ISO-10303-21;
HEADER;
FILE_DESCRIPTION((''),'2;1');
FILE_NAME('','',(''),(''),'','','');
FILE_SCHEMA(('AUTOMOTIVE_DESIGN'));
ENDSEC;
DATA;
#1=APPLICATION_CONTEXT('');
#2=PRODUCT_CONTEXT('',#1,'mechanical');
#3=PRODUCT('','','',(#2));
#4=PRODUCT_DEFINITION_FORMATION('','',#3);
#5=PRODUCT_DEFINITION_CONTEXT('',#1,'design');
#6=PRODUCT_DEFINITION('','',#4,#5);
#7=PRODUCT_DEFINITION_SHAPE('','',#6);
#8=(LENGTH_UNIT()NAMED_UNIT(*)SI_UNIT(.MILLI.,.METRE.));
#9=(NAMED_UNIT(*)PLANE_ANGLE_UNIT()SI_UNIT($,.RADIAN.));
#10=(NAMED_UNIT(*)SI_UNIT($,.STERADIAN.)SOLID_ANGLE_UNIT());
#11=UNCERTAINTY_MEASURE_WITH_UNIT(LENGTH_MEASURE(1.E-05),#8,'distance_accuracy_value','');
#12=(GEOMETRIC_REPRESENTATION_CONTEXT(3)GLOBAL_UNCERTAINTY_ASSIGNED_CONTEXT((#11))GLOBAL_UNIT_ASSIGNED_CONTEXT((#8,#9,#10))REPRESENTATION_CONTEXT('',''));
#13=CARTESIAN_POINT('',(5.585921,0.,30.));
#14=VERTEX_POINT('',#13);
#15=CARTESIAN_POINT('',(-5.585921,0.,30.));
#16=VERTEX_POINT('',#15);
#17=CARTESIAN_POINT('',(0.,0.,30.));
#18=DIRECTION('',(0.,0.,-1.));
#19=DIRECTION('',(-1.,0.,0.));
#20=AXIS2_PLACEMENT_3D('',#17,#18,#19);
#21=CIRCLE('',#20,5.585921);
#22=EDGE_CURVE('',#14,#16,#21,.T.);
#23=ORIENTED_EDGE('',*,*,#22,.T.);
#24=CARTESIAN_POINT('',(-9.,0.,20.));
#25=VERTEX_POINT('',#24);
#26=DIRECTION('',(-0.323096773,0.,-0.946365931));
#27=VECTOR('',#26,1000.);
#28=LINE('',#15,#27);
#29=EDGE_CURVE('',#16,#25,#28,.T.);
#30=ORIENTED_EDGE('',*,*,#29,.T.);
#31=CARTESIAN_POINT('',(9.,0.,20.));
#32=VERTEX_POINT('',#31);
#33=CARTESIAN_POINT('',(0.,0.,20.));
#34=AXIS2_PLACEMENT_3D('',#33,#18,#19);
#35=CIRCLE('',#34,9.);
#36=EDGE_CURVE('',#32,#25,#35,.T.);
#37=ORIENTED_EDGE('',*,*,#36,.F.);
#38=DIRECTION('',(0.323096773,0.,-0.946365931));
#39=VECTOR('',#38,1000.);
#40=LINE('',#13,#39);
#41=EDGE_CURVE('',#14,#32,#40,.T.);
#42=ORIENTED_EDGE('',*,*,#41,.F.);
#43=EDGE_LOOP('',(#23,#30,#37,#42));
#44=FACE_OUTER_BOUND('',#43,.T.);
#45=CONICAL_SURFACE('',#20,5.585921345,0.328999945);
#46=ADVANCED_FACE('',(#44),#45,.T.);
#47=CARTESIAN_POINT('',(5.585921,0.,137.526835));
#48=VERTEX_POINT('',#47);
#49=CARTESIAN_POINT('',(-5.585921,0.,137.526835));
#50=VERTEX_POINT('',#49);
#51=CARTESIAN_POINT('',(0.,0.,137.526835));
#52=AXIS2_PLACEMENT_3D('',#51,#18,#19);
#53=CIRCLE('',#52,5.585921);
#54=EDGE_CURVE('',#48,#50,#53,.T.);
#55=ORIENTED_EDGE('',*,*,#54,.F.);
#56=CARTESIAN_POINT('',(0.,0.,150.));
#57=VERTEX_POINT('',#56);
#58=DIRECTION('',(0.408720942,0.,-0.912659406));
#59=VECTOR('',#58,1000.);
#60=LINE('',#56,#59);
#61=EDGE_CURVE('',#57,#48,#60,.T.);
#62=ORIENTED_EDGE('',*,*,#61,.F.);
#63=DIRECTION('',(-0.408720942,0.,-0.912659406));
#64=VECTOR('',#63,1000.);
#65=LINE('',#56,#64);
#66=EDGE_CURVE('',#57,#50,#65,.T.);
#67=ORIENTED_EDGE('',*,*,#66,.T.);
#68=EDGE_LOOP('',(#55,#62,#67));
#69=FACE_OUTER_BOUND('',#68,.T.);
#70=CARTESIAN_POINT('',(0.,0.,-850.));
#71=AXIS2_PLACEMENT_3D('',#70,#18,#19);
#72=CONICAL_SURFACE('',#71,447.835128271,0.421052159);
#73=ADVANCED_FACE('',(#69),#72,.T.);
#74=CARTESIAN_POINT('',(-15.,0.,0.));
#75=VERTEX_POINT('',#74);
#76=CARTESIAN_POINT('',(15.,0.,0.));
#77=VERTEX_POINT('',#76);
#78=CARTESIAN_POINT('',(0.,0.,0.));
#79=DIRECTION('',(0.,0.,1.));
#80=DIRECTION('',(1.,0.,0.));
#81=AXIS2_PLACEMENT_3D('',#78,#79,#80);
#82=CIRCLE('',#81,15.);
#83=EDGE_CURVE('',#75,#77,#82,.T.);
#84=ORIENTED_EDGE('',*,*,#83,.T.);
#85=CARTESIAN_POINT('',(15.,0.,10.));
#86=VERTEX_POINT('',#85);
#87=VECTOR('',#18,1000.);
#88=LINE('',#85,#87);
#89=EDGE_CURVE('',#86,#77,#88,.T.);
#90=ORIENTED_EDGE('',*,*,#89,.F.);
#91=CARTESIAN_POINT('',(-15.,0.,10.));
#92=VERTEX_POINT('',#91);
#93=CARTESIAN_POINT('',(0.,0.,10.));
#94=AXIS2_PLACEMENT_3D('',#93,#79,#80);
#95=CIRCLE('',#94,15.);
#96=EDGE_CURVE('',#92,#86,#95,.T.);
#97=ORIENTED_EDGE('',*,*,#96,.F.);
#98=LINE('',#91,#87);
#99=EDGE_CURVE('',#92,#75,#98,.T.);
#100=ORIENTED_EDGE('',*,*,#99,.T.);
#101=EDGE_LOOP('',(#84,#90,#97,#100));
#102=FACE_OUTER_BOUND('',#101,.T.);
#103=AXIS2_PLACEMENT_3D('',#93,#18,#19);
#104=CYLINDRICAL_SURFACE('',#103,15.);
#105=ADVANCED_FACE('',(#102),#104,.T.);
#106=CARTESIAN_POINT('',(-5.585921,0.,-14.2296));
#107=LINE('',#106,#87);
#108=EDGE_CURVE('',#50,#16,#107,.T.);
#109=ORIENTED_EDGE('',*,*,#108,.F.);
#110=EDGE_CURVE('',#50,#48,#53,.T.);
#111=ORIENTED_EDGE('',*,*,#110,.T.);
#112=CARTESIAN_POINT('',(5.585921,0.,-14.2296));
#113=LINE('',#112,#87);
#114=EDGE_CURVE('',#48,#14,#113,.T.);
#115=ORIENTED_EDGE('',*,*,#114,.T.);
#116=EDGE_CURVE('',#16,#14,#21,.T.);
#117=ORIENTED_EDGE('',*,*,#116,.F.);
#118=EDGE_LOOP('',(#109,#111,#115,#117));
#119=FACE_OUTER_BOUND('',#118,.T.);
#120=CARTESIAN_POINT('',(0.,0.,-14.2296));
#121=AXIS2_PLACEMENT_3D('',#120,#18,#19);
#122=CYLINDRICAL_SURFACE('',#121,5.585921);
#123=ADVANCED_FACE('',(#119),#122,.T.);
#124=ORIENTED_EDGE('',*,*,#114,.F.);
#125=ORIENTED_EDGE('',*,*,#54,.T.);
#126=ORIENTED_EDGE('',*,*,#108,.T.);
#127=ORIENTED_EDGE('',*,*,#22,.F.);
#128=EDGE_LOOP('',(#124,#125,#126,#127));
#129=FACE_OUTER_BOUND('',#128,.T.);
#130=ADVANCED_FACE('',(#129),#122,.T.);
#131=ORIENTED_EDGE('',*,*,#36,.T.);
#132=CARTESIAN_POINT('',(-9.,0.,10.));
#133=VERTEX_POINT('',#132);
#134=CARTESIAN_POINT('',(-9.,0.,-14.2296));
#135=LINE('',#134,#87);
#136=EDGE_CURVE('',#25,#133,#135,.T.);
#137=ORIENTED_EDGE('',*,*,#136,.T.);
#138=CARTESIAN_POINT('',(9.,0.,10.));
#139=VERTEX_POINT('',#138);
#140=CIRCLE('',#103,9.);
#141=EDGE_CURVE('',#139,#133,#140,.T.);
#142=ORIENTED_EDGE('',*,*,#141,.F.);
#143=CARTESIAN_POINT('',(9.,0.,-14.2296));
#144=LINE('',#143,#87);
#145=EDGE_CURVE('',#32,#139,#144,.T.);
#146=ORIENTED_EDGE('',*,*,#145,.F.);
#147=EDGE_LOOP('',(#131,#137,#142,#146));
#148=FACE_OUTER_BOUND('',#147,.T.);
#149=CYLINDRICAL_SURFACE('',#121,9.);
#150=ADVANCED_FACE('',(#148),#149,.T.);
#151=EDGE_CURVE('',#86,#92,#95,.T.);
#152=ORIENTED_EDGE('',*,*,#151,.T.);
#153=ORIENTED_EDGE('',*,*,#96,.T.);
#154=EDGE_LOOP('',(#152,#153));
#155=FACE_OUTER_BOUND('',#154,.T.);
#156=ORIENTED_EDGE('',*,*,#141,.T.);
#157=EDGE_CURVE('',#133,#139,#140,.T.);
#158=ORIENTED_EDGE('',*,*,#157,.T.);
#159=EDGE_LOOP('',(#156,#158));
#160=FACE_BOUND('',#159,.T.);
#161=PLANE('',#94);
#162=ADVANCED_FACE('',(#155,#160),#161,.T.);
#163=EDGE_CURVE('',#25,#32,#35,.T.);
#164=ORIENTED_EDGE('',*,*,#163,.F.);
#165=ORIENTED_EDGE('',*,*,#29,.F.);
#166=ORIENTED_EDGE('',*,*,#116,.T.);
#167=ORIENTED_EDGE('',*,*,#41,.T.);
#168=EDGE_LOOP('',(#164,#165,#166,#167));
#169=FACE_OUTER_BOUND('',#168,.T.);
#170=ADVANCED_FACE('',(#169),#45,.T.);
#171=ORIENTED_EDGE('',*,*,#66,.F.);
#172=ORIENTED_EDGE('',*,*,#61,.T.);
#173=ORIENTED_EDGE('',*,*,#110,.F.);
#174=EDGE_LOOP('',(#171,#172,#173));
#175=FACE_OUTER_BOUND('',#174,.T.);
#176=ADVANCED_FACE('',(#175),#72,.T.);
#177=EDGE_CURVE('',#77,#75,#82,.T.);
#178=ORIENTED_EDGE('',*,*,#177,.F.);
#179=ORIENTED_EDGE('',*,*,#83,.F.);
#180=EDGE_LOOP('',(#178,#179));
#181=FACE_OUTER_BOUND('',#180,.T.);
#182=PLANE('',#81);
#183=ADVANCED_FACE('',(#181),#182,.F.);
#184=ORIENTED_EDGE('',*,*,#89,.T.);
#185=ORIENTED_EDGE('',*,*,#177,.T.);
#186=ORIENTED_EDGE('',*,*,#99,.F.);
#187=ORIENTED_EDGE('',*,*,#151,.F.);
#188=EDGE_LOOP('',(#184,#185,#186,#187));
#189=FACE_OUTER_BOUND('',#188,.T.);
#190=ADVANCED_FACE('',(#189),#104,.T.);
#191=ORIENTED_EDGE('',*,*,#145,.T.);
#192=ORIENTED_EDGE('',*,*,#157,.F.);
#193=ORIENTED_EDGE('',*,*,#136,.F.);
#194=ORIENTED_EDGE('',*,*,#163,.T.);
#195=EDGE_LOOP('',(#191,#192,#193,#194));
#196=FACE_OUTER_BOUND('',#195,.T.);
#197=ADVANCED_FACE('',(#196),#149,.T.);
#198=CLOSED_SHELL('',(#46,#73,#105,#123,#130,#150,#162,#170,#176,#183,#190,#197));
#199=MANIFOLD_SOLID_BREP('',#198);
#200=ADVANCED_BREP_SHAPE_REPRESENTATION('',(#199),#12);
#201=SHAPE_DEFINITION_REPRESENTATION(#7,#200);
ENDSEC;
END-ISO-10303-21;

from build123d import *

# Parameters (mm, degrees)
SKETCH1_R           = 15
BOSS_EXTRUDE1_DEPTH = 10


with BuildPart() as part:
    # Sketch1 → Boss-Extrude1 (new body)
    with BuildSketch(Plane.XY):
        Circle(SKETCH1_R)
    extrude(amount=BOSS_EXTRUDE1_DEPTH)

    # Sketch2 → Revolve1 (revolve)
    with BuildSketch(Plane(origin=(0, 0, 0), x_dir=(1, 0, 0), z_dir=(0, 1, 0)), mode=Mode.PRIVATE) as revolve1_sk:
        Polygon((9, -10), (9, -20), (5.585921345, -30), (5.585921345, -137.526835229), (0, -150), (0, -10), align=None)
    revolve(revolve1_sk.sketch.rotate(Axis((0, 0, -14.229599779), (0, 0, 1)), 180), axis=Axis((0, 0, -14.229599779), (0, 0, 1)))


solid = part.part
